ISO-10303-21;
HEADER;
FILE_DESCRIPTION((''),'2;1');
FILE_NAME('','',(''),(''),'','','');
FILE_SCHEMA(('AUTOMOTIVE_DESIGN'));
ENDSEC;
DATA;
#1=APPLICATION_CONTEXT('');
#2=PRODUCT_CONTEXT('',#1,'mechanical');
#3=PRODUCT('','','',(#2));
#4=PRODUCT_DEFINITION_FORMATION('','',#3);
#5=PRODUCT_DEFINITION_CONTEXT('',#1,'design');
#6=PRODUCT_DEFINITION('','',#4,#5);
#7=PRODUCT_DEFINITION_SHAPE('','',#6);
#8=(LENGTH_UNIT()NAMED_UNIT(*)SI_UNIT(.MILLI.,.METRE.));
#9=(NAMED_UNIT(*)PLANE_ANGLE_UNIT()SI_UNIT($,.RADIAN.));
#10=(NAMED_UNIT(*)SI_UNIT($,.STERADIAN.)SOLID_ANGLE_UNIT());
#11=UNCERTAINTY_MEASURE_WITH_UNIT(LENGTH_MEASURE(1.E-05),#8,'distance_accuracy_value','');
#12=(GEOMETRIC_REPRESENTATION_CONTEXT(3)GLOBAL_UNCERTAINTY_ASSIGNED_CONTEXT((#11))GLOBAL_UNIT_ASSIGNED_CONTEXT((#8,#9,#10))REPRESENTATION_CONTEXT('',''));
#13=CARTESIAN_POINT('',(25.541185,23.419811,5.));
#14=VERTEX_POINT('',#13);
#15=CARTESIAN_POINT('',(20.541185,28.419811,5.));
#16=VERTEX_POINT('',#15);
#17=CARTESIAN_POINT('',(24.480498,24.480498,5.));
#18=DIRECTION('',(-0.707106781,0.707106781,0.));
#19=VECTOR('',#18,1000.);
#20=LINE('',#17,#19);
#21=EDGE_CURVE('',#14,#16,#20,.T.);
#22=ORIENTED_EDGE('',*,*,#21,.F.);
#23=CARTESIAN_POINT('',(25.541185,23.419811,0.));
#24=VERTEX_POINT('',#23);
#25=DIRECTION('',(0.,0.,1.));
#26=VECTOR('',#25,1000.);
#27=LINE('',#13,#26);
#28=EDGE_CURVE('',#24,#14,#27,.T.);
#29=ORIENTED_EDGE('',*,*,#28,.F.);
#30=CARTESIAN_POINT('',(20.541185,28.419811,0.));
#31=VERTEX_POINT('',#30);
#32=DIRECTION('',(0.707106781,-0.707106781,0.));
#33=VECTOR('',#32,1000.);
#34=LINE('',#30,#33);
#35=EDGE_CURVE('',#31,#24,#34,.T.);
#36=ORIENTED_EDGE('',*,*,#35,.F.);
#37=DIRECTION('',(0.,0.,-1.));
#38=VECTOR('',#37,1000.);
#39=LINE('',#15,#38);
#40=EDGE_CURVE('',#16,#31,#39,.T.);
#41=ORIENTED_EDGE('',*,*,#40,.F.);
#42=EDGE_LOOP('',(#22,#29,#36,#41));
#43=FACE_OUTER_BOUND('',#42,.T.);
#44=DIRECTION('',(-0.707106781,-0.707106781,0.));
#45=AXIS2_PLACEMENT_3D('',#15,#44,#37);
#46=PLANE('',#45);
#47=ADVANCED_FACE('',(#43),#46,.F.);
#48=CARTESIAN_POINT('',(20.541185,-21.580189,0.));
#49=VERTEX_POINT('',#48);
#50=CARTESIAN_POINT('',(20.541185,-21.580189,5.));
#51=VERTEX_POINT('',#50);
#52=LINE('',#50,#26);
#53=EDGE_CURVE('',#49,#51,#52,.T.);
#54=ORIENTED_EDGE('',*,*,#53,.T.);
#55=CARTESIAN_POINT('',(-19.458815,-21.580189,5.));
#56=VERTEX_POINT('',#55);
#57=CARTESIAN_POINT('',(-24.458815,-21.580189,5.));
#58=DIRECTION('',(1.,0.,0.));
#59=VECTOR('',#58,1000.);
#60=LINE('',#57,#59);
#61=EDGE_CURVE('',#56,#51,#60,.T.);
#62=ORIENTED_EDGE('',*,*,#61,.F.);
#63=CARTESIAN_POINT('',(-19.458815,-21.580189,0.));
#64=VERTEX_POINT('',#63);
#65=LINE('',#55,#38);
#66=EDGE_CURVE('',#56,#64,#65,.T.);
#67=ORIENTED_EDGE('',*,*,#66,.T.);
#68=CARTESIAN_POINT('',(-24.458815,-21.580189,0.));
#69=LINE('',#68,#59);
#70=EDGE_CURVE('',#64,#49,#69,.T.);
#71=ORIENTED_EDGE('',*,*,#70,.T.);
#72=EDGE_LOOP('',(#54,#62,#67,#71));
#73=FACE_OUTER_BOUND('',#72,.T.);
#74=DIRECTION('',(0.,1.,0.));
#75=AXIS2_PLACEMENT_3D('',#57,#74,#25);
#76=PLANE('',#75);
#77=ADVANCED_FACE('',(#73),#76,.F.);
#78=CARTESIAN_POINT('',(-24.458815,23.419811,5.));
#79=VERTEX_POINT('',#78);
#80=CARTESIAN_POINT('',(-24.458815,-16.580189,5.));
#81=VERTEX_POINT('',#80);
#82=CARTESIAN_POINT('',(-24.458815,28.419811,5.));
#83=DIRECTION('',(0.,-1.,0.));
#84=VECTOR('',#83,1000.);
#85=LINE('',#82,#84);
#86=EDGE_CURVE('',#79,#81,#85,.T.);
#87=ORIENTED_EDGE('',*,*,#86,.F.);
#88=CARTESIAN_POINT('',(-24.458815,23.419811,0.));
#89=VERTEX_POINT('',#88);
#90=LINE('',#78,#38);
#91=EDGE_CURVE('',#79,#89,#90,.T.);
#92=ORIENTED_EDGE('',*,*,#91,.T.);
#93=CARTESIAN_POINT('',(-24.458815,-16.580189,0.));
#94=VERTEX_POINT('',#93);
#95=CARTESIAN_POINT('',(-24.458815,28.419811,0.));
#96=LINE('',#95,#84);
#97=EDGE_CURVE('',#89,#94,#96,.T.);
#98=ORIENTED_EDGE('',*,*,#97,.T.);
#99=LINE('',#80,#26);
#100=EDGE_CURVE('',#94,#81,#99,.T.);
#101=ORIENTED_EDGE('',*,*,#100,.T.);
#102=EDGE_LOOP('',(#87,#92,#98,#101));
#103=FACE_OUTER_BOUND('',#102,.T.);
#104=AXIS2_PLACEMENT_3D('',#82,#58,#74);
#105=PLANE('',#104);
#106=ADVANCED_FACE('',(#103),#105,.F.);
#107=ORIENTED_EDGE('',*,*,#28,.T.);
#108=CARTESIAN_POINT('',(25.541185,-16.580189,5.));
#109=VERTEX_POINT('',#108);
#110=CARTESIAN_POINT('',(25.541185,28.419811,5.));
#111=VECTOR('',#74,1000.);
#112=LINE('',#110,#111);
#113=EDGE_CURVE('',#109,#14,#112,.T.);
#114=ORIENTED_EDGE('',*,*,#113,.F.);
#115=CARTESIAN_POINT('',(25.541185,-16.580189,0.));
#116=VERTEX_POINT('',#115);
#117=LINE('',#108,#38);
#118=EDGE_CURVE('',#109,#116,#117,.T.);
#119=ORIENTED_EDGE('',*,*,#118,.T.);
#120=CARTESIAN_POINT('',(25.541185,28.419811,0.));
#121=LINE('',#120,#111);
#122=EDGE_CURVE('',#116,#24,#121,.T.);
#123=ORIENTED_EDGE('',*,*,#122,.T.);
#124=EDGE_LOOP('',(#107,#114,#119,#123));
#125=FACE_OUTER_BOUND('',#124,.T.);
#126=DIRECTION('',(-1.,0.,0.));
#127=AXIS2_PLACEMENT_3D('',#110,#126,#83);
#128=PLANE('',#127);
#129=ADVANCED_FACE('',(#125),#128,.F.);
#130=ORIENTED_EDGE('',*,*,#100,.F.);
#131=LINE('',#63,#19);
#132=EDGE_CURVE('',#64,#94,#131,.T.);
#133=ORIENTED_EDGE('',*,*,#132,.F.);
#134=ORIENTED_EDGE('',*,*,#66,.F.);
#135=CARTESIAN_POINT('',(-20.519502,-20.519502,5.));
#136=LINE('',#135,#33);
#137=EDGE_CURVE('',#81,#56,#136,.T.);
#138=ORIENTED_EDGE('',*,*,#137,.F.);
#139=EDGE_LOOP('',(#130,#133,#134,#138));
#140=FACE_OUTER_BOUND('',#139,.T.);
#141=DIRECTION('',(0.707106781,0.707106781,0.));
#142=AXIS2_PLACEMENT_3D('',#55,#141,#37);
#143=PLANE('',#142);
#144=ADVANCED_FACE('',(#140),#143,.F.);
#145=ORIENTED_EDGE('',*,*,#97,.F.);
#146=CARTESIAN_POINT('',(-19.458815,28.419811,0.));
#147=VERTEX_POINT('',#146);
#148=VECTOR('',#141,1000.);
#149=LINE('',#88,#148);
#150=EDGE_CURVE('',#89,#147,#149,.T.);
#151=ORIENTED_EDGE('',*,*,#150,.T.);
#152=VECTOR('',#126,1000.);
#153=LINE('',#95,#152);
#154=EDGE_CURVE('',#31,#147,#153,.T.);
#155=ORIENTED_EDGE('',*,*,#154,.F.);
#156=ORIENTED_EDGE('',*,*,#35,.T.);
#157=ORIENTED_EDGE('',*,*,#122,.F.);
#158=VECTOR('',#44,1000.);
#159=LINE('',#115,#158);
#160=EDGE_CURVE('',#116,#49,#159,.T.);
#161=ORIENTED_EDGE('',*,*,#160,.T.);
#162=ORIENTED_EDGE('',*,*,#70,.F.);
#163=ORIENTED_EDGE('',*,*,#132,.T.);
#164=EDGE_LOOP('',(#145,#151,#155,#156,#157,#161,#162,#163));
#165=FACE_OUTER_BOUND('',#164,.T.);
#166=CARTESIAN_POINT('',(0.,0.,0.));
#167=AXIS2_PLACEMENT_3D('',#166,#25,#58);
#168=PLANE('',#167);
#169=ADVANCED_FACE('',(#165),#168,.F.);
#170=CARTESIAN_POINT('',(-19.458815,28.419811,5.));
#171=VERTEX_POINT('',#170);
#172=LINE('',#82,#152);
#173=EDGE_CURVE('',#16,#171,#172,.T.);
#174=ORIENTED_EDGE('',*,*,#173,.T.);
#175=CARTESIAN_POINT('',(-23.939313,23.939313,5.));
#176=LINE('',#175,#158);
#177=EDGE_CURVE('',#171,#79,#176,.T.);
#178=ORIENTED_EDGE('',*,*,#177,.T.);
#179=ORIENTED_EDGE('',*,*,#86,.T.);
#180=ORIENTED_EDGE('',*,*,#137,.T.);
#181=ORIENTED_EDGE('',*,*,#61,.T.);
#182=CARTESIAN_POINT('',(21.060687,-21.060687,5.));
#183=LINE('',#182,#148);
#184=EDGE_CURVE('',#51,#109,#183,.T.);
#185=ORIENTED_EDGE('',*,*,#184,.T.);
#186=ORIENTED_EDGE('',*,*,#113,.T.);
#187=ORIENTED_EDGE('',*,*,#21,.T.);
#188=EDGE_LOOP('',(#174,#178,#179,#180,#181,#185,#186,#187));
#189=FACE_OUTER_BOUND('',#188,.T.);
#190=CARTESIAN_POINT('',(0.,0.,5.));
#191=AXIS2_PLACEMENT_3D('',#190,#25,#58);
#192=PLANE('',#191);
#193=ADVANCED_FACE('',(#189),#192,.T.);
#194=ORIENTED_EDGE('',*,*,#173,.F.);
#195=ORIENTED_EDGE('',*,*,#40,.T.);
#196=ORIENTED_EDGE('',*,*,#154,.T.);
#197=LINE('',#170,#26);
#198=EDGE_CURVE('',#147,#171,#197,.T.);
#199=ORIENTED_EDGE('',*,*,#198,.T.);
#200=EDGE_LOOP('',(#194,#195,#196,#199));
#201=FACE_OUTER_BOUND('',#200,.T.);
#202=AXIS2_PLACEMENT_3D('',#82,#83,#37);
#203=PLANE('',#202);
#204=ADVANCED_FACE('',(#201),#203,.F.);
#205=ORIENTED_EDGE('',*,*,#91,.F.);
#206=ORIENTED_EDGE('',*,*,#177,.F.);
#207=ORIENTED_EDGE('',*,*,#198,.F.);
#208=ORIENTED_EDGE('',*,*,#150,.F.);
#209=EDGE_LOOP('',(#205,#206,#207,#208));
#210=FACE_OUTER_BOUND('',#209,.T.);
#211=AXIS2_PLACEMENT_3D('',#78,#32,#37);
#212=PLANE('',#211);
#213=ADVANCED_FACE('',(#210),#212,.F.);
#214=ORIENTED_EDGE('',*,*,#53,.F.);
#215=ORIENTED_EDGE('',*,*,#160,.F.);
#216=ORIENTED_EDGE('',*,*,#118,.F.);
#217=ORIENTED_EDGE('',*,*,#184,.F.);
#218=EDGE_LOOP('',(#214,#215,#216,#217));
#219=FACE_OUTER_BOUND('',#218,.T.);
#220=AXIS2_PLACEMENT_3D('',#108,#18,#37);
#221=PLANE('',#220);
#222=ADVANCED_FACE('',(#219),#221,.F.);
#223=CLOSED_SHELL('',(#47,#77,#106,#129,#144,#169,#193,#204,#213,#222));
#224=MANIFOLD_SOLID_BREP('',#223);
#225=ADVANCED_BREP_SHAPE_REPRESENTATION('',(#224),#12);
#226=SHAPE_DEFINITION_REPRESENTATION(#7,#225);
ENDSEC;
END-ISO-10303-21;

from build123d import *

# Parameters (mm, degrees)
SKETCH1_W           = 50
SKETCH1_H           = 50
BOSS_EXTRUDE1_DEPTH = 5
CHAMFER1_SIZE       = 5


with BuildPart() as part:
    # Sketch1 → Boss-Extrude1 (new body)
    with BuildSketch(Plane.XY):
        with Locations((0.541184779, 3.419811321)):
            Rectangle(SKETCH1_W, SKETCH1_H)
    extrude(amount=BOSS_EXTRUDE1_DEPTH)

    # Chamfer1
    chamfer1_edges = [part.edges().sort_by_distance(p)[0] for p in [
        (-24.458815221, 28.419811321, 2.5),
        (25.541184779, 28.419811321, 2.5),
        (25.541184779, -21.580188679, 2.5),
        (-24.458815221, -21.580188679, 2.5),
    ]]
    chamfer(chamfer1_edges, length=CHAMFER1_SIZE)


solid = part.part
